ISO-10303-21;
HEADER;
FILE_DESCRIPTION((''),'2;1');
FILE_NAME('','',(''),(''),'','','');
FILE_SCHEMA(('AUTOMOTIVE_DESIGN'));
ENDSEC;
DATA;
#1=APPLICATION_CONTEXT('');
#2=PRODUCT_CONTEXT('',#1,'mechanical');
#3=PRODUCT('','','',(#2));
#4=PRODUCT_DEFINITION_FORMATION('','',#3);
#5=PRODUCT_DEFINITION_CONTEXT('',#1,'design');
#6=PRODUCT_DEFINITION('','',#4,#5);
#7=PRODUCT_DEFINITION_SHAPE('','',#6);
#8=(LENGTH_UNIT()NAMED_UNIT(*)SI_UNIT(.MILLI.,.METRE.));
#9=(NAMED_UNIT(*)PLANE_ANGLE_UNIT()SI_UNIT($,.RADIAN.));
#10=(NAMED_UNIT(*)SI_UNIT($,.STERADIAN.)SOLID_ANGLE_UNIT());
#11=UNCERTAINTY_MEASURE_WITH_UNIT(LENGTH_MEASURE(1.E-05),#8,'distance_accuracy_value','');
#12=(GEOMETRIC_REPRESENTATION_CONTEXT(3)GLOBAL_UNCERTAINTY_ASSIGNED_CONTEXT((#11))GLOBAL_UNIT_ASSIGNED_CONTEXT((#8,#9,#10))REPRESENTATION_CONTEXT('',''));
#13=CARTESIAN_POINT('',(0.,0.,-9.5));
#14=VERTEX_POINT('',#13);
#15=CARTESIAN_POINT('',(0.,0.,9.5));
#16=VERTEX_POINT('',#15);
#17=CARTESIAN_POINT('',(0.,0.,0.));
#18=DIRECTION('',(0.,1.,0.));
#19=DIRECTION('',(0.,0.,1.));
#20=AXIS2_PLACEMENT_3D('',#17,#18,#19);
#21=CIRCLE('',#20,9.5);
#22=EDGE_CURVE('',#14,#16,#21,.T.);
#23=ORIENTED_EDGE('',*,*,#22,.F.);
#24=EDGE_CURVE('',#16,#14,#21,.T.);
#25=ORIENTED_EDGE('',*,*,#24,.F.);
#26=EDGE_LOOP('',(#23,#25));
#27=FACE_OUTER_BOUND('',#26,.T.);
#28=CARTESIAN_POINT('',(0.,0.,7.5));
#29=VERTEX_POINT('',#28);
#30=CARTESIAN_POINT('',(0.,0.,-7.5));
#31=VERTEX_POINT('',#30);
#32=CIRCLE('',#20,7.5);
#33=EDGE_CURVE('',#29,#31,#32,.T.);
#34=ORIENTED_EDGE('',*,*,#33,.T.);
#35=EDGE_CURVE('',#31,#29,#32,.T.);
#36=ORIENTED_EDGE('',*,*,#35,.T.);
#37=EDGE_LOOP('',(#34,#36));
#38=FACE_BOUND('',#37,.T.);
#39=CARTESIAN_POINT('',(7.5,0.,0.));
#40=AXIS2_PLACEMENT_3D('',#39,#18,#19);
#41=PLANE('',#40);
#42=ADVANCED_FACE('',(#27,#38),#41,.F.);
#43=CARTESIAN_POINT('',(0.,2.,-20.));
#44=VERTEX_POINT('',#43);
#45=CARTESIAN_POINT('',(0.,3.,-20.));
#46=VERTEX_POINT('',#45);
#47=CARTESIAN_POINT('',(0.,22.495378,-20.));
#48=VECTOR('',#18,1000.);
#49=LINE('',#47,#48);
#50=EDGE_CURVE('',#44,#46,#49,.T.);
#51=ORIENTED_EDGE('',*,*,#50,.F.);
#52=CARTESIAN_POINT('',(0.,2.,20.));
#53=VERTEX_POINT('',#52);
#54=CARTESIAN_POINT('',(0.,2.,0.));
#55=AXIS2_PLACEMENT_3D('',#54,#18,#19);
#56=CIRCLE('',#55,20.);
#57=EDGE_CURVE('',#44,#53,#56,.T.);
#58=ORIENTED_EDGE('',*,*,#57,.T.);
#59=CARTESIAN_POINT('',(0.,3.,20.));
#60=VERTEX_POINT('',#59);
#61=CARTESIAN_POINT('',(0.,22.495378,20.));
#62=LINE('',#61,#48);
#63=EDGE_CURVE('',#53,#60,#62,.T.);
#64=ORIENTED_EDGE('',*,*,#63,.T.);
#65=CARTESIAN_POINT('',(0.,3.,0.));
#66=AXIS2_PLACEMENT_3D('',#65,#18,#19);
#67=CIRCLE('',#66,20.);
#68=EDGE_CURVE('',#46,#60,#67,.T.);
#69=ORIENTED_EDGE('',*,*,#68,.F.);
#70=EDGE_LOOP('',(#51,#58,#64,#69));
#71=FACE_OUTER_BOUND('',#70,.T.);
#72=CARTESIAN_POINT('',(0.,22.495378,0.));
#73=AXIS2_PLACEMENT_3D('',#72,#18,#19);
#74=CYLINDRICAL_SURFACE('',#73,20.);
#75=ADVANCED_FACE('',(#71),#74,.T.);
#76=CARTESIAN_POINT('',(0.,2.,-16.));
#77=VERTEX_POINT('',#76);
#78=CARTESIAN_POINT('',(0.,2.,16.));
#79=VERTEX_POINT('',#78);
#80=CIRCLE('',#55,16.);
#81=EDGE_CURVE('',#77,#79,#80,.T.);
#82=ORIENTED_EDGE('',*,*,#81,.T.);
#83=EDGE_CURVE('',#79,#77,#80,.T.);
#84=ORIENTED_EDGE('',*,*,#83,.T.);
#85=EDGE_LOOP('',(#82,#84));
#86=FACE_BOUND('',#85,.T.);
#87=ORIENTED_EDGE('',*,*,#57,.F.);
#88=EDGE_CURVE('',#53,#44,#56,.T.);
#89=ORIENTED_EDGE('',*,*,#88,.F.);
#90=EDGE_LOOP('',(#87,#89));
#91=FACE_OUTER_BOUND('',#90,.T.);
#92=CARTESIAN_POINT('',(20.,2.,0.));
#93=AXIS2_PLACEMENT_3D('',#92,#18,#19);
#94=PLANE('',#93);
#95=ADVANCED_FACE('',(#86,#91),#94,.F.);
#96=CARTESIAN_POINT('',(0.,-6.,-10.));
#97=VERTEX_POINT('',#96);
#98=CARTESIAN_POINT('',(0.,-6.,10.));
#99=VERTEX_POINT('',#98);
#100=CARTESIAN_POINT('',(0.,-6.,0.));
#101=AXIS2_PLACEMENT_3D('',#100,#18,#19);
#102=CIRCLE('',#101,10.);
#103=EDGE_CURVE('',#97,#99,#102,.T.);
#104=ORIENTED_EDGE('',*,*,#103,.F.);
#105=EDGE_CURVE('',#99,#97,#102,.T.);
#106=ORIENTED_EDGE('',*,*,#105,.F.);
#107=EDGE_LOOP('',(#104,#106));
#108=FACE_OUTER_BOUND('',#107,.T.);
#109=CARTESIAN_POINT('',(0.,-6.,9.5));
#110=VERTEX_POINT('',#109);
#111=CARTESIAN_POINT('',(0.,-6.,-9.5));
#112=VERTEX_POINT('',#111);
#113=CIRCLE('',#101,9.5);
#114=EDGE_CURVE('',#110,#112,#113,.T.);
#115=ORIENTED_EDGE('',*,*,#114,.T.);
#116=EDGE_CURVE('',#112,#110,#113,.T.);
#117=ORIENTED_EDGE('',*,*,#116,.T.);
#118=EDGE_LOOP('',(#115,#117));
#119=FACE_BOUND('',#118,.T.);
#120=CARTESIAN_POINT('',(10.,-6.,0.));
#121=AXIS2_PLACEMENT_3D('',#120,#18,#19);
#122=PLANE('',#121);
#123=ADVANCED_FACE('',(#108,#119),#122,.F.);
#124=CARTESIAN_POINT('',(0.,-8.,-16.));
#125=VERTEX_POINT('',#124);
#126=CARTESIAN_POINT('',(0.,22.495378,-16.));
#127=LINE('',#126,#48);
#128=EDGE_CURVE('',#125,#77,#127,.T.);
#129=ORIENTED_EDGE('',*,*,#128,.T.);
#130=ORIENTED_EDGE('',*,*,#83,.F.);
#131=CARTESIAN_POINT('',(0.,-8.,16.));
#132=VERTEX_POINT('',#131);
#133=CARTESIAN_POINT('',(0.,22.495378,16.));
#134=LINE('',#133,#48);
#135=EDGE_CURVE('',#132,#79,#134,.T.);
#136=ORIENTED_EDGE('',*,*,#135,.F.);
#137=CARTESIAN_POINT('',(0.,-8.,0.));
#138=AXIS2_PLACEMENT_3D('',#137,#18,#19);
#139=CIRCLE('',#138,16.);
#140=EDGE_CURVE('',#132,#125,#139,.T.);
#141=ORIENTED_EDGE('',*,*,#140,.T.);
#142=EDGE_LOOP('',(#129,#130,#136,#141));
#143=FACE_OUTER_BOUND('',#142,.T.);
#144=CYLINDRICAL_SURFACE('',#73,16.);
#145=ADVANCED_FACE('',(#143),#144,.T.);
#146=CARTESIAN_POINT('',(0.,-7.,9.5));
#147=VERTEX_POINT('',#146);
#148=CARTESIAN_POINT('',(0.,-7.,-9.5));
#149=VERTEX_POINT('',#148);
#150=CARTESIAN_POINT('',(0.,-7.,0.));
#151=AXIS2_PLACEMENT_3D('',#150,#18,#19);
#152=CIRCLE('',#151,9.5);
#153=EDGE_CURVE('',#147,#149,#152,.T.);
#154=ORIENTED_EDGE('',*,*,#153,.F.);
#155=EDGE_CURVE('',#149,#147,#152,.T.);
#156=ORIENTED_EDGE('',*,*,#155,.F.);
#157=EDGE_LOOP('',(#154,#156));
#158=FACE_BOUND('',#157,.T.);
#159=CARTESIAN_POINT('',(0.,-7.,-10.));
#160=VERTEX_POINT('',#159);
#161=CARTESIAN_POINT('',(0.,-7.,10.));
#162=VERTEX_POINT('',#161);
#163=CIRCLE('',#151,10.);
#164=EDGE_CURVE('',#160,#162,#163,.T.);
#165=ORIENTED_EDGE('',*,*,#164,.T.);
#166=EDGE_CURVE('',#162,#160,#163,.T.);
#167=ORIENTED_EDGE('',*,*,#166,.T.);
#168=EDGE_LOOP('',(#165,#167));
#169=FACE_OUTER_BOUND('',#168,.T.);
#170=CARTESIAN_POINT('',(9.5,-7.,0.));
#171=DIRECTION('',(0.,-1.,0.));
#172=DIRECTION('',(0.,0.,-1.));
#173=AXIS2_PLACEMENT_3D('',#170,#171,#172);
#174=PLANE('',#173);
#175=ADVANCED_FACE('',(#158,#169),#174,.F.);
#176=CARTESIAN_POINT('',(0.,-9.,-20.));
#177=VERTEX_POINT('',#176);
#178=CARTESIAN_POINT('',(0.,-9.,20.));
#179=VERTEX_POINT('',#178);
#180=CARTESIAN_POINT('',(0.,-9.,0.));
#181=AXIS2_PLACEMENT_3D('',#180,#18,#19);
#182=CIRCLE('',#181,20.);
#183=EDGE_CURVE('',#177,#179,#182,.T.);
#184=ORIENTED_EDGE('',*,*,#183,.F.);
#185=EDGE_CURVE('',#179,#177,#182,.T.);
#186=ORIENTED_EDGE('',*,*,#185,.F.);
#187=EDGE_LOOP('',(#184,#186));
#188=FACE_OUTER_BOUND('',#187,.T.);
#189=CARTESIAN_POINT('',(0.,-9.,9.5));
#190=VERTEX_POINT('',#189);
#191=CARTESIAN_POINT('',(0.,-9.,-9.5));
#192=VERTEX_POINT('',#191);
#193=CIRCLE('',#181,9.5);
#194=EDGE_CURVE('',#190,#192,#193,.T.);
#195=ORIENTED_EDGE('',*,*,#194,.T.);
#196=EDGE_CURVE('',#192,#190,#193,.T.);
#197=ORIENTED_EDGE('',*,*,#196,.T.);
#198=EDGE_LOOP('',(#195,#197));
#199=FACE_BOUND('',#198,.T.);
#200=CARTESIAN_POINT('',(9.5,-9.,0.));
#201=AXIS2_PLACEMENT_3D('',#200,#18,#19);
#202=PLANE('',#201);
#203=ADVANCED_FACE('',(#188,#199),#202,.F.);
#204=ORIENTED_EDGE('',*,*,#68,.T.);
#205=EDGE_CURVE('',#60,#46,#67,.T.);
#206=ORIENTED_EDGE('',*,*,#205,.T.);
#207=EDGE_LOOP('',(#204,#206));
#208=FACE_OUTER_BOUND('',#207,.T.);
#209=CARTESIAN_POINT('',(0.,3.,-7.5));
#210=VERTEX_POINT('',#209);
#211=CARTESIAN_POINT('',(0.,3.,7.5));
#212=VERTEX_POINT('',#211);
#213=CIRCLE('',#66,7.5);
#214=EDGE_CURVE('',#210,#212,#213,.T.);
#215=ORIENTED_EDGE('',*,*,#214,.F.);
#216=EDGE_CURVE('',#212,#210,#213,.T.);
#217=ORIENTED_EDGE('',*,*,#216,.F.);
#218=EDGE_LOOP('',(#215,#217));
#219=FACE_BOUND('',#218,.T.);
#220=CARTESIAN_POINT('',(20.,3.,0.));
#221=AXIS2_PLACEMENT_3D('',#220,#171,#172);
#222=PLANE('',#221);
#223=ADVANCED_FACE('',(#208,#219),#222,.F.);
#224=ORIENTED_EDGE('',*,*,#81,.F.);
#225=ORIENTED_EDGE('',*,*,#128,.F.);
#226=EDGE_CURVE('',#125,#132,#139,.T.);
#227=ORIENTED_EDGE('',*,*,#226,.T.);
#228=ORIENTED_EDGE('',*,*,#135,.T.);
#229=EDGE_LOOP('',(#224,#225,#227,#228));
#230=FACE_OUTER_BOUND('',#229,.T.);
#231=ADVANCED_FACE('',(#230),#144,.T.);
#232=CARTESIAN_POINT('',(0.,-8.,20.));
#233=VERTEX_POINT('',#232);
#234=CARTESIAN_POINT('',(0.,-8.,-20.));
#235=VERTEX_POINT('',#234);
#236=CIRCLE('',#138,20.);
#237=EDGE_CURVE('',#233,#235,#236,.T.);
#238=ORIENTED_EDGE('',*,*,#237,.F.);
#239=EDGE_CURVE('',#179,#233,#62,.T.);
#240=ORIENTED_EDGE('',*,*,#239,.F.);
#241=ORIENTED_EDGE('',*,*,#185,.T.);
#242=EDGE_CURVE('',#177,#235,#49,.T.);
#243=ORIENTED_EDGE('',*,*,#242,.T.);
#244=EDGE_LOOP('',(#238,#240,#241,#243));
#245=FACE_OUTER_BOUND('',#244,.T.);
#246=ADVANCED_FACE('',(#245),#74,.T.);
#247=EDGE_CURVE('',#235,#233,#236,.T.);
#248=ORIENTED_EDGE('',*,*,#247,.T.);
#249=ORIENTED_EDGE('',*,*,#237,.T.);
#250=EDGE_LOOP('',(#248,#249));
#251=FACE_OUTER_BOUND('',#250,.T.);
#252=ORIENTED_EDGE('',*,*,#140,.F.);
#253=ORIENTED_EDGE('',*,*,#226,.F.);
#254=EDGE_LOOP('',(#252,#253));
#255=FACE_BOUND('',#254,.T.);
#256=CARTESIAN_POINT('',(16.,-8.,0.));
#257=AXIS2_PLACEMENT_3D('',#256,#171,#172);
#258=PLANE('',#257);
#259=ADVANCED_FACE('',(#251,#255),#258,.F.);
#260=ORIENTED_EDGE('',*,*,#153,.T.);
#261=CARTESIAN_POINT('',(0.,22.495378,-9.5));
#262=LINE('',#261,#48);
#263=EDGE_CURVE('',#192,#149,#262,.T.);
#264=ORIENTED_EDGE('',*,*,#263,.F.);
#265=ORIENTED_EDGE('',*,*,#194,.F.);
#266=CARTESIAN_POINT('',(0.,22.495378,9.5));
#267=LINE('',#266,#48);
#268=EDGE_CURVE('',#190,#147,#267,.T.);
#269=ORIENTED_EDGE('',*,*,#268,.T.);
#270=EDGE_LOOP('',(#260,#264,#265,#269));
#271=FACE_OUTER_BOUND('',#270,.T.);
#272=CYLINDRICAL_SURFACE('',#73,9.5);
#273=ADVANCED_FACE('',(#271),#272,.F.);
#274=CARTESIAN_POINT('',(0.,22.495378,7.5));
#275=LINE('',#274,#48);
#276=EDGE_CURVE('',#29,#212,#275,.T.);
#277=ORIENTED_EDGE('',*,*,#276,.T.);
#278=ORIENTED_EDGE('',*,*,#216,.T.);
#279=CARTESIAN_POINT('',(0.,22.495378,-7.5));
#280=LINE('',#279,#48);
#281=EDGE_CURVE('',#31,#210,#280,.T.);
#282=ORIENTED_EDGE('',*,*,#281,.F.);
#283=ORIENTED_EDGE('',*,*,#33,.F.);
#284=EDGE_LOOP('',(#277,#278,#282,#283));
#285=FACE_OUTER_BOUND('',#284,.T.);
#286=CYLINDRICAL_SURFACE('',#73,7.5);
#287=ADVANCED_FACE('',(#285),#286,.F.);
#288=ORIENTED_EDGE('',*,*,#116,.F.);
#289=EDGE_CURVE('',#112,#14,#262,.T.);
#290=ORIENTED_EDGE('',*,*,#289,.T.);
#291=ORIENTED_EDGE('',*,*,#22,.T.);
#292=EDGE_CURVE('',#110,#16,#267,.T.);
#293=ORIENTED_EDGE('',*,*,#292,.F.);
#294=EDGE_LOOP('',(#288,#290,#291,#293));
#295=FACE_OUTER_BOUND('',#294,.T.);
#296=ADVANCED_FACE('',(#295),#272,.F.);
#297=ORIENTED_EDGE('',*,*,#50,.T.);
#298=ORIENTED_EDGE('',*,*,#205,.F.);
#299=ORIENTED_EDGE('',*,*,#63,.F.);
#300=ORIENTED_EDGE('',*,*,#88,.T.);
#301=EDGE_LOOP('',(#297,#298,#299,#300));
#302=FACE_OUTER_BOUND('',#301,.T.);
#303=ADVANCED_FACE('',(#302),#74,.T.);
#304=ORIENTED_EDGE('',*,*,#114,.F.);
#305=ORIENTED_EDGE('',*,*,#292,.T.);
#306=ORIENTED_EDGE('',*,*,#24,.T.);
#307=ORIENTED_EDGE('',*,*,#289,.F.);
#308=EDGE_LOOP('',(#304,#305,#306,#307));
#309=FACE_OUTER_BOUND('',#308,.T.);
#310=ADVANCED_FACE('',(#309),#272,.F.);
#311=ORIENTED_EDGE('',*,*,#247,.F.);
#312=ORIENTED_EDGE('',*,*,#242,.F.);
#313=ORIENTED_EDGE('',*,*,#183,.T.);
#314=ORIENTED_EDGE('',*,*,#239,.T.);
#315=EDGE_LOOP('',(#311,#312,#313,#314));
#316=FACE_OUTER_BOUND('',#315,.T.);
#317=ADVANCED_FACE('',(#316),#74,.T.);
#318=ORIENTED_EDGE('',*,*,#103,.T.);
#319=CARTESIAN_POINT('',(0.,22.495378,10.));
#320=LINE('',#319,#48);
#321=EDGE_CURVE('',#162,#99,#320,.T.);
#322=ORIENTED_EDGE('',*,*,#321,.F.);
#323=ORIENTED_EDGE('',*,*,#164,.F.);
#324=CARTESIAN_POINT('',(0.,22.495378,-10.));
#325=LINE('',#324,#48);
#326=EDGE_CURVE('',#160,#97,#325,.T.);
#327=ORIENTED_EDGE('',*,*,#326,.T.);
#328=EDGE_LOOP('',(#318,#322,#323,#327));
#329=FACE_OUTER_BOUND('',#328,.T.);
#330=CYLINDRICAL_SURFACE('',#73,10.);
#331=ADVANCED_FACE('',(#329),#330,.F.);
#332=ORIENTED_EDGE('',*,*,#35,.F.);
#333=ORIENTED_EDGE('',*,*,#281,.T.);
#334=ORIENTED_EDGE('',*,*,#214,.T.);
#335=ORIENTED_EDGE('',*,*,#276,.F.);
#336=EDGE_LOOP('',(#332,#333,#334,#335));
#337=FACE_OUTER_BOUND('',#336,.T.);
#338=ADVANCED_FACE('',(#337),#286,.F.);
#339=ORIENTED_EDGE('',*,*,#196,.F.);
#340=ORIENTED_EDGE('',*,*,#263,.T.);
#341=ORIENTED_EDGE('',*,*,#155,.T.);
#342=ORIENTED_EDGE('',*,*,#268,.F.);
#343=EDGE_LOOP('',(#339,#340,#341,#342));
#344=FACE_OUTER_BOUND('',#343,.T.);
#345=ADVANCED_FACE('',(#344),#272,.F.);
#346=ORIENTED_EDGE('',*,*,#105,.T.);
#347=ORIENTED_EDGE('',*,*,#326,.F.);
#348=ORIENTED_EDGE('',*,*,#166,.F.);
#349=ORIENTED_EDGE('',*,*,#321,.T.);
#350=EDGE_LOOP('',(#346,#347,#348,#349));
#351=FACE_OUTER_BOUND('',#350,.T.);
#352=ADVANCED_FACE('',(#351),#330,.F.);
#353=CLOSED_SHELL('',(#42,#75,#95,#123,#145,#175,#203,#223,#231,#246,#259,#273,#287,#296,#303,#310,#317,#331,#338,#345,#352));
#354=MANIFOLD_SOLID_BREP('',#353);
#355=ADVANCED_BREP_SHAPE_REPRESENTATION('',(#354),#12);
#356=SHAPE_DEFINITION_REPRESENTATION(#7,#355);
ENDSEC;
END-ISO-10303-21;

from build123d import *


with BuildPart() as part:
    # 草图1 → 旋转1 (revolve)
    with BuildSketch(Plane.XY, mode=Mode.PRIVATE) as revolve_1_sk:
        Polygon((7.5, 3), (7.5, 0), (9.5, 0), (9.5, -6), (10, -6), (10, -7), (9.5, -7), (9.5, -9), (20, -9), (20, -8), (16, -8), (16, 2), (20, 2), (20, 3), align=None)
    revolve(revolve_1_sk.sketch.rotate(Axis((0, 22.495377882, 0), (0, -1, 0)), 90), axis=Axis((0, 22.495377882, 0), (0, -1, 0)))


solid = part.part
